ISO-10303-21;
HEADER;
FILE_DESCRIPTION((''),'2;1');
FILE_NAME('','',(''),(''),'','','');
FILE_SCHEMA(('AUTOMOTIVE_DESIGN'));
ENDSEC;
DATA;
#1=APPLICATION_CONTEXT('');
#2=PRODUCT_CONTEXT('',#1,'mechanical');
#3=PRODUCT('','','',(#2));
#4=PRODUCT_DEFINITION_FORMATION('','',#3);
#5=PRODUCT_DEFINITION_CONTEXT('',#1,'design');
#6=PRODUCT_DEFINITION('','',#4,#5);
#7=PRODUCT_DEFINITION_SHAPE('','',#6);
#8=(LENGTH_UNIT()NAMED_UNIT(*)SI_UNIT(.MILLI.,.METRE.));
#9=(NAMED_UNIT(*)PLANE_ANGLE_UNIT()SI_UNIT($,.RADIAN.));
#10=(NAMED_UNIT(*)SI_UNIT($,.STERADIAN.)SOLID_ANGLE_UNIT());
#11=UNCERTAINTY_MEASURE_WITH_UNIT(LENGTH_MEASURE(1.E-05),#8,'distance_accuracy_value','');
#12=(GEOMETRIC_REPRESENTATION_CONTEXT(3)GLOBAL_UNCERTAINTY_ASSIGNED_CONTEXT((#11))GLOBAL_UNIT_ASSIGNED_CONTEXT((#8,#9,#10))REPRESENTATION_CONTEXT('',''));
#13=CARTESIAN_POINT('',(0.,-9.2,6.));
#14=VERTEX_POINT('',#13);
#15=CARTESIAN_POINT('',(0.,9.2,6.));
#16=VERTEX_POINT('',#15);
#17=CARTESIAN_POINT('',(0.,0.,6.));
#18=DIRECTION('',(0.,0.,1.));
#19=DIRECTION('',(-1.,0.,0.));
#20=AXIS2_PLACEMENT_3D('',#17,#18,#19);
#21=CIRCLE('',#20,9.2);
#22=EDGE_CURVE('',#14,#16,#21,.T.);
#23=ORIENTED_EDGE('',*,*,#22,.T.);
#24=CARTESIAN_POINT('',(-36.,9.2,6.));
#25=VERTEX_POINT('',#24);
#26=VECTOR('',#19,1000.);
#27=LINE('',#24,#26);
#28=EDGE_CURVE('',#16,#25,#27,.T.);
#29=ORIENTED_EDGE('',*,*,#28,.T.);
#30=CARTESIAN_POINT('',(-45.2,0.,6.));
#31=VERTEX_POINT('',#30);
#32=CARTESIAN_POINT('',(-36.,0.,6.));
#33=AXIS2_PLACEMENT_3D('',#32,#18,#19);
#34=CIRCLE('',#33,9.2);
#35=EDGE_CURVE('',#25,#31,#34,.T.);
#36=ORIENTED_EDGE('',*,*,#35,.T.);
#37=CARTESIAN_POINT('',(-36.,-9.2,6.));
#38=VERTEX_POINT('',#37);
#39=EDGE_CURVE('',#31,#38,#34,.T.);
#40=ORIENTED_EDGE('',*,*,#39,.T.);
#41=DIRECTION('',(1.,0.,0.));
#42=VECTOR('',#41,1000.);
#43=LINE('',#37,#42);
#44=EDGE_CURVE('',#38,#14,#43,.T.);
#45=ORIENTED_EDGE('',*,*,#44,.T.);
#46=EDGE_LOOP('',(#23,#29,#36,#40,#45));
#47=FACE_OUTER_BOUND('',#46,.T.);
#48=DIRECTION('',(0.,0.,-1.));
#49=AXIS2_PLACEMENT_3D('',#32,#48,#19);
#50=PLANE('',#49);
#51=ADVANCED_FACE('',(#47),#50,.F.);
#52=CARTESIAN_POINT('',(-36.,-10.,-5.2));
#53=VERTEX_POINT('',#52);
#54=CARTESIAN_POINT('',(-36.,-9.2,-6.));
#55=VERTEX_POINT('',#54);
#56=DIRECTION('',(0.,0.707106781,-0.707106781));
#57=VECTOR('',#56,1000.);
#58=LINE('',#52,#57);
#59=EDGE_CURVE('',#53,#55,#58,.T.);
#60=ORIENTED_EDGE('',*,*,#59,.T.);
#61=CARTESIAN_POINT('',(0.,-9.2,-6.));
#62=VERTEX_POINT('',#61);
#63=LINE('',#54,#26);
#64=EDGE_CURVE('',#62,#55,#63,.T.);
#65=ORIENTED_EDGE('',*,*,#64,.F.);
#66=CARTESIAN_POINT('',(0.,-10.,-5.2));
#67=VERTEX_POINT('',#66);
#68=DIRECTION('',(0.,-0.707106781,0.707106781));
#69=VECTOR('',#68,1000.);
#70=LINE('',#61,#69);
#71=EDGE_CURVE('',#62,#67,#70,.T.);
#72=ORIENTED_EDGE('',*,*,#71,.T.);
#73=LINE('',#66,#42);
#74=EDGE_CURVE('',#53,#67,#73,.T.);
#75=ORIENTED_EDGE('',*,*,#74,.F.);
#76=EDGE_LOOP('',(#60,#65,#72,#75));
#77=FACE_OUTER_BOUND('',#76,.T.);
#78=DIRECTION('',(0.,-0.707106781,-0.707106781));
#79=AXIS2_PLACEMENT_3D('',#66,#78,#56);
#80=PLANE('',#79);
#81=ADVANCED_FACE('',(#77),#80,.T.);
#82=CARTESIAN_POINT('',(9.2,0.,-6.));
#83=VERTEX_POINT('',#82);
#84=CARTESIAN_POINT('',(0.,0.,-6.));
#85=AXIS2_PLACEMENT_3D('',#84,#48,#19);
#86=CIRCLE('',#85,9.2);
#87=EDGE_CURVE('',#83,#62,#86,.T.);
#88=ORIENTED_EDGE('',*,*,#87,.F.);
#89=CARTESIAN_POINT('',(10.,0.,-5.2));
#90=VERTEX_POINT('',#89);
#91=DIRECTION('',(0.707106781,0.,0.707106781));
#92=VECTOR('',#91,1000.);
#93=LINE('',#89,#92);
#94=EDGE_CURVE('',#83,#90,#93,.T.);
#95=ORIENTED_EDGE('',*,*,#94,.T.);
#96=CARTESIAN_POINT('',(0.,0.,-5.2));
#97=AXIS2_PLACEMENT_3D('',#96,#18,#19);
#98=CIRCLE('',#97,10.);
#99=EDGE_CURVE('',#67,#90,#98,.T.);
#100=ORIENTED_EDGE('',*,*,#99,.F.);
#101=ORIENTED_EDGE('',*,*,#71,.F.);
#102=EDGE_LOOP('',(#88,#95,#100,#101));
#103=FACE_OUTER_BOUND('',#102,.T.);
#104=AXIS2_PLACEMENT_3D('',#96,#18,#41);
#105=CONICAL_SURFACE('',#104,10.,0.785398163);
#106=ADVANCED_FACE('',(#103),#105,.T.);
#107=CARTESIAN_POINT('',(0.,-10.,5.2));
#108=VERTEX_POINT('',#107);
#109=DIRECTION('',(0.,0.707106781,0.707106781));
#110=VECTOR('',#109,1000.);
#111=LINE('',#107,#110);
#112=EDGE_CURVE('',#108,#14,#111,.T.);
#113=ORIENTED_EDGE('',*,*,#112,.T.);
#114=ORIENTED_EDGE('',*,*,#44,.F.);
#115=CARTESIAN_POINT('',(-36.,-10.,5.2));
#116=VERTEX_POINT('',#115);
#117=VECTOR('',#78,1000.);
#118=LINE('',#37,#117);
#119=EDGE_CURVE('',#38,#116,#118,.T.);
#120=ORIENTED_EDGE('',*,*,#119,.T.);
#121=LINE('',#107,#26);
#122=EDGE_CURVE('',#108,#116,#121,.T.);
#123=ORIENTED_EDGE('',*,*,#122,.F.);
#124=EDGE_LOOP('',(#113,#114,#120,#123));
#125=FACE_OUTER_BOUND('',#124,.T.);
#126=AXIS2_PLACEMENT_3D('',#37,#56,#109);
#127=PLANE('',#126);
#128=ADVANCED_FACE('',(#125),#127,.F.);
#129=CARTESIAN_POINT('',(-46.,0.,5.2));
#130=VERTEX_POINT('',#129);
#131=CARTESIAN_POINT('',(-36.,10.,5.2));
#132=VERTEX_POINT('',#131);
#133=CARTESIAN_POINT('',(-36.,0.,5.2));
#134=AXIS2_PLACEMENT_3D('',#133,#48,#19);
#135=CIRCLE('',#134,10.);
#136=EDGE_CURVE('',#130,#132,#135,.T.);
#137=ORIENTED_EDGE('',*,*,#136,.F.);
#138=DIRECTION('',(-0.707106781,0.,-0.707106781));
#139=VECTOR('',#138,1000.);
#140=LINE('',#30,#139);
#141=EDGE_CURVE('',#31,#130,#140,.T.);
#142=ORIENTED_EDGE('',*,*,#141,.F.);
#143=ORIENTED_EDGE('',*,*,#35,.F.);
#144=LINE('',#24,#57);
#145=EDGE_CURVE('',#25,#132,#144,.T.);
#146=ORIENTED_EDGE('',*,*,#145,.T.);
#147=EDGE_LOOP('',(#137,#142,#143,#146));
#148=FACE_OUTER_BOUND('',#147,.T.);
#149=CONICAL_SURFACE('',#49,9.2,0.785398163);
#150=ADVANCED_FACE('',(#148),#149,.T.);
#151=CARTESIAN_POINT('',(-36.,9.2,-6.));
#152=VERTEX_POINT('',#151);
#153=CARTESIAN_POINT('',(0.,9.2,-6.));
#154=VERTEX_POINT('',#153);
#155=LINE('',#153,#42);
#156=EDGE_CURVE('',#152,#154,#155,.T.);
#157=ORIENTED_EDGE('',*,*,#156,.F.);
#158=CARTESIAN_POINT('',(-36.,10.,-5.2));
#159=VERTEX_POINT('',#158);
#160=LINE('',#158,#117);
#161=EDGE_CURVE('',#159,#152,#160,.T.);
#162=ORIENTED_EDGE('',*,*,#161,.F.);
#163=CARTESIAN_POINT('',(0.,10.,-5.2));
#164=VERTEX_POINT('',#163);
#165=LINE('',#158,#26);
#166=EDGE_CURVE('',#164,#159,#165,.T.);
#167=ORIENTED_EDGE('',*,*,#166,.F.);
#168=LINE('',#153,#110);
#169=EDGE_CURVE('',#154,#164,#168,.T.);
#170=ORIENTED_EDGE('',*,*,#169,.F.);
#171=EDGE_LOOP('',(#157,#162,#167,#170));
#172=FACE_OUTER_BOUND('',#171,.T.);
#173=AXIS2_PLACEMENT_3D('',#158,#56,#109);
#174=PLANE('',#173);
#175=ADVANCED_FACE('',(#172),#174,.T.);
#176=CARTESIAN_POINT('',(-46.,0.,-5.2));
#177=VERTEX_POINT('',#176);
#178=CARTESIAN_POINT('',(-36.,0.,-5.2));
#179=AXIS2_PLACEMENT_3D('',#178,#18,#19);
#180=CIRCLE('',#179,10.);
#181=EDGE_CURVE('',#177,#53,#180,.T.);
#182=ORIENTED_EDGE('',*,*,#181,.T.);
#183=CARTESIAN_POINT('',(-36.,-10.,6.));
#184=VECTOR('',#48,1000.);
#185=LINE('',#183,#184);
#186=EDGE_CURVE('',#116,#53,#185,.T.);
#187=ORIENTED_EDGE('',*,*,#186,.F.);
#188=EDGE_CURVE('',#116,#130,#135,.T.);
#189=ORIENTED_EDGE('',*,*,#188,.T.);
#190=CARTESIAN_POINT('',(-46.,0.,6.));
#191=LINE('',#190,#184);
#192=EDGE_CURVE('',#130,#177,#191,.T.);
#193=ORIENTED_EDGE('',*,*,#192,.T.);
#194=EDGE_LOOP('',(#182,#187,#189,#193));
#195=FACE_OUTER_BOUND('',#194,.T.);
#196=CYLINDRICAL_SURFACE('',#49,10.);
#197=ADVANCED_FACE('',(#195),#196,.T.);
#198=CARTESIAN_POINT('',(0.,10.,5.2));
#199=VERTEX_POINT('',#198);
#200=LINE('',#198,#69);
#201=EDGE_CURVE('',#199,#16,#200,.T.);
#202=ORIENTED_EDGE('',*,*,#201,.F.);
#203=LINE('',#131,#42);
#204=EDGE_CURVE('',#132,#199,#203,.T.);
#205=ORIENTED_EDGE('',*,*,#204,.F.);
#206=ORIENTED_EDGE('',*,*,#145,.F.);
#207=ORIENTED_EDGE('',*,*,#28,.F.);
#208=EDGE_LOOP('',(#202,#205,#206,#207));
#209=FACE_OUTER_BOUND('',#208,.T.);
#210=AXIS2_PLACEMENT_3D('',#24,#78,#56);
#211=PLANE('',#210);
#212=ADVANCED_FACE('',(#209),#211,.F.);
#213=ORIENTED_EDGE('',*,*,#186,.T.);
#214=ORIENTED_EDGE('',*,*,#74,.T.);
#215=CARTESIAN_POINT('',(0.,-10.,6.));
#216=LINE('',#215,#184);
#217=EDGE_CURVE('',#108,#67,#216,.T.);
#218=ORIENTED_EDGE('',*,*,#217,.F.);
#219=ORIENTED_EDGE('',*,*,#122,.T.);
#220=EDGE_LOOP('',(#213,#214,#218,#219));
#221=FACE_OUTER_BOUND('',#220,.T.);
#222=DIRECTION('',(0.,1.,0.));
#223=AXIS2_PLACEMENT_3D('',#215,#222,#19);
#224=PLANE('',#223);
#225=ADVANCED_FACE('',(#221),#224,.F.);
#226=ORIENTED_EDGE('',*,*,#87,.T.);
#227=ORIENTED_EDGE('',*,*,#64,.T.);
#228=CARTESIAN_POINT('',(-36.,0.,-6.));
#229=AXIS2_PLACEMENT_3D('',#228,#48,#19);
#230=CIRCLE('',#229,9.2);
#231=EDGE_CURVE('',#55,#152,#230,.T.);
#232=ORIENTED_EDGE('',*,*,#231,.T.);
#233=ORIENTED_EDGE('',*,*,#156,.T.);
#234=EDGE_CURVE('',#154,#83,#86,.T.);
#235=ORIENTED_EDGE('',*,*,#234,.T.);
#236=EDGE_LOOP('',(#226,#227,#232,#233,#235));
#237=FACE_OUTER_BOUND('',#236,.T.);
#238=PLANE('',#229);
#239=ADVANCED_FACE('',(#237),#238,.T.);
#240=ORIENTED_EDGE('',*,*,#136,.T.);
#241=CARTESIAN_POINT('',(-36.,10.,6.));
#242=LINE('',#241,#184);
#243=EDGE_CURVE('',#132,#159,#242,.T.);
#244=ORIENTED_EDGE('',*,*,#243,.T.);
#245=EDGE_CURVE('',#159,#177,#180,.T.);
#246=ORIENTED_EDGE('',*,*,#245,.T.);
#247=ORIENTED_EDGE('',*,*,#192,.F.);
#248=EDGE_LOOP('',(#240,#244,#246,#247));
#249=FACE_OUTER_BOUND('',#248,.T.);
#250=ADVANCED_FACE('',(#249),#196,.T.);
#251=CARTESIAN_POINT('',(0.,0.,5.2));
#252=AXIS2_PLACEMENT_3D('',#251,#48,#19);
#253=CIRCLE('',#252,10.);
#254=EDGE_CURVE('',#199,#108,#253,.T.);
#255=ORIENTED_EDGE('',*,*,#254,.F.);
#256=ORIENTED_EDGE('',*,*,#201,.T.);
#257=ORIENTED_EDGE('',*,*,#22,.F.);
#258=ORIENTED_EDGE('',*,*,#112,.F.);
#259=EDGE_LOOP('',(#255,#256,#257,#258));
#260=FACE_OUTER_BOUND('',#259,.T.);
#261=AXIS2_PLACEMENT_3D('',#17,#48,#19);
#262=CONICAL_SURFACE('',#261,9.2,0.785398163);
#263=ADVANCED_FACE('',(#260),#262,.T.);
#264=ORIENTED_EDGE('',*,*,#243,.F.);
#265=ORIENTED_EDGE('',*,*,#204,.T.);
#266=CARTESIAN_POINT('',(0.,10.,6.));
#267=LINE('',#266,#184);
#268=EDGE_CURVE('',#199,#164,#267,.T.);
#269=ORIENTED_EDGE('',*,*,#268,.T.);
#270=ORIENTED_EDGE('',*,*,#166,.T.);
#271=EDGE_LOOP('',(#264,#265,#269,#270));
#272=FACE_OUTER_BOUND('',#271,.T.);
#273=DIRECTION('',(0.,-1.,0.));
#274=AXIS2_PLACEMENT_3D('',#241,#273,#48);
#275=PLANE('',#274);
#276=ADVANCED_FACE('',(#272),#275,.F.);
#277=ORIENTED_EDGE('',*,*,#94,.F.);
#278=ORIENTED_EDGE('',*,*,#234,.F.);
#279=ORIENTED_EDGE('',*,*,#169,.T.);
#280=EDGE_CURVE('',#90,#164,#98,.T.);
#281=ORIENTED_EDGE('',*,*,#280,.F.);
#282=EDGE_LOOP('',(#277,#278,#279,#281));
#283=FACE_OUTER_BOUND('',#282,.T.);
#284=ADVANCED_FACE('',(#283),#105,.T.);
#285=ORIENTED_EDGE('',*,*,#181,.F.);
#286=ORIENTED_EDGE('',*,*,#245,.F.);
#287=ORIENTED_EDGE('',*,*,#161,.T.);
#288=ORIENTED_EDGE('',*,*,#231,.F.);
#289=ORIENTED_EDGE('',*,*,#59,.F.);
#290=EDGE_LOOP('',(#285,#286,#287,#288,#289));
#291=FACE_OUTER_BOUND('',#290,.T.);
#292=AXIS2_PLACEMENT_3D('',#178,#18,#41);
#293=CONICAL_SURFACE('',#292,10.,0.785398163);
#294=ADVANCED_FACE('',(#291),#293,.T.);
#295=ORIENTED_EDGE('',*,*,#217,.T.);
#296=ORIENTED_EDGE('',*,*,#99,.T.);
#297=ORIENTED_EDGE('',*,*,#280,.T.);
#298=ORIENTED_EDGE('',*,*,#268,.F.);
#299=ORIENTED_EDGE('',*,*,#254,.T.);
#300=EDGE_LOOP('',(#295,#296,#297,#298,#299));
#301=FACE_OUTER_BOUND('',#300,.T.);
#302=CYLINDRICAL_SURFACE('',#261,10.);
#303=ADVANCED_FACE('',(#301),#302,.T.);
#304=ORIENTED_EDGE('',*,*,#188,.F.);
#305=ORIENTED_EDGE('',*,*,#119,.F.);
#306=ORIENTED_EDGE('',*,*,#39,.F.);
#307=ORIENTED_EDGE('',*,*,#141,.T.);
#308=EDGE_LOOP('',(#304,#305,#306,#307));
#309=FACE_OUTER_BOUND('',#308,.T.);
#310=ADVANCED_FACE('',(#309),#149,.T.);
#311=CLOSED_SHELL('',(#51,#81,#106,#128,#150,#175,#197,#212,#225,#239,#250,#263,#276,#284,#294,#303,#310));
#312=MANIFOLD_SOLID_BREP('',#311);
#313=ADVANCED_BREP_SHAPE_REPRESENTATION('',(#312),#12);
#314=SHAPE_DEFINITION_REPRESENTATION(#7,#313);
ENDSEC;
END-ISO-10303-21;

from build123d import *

# Parameters (mm, degrees)
BASEKEY_DEPTH = 6
CHAMFER1_SIZE = 0.8


with BuildPart() as part:
    # Sketch1 → BaseKey (new, symmetric)
    with BuildSketch(Plane.XY):
        with BuildLine():
            Line((-36, 10), (0, 10))
            ThreePointArc((0, 10), (10, 0), (0, -10))
            Line((0, -10), (-36, -10))
            ThreePointArc((-36, -10), (-46, 0), (-36, 10))
        make_face()
    extrude(amount=BASEKEY_DEPTH, both=True)

    # Chamfer1
    chamfer1_edges = [part.edges().sort_by_distance(p)[0] for p in [
        (10, 0, 6),
        (-18, 10, 6),
        (-46, 0, 6),
        (-18, 10, -6),
        (10, 0, -6),
        (-18, -10, -6),
        (-46, 0, -6),
        (-18, -10, 6),
    ]]
    chamfer(chamfer1_edges, length=CHAMFER1_SIZE)


solid = part.part
